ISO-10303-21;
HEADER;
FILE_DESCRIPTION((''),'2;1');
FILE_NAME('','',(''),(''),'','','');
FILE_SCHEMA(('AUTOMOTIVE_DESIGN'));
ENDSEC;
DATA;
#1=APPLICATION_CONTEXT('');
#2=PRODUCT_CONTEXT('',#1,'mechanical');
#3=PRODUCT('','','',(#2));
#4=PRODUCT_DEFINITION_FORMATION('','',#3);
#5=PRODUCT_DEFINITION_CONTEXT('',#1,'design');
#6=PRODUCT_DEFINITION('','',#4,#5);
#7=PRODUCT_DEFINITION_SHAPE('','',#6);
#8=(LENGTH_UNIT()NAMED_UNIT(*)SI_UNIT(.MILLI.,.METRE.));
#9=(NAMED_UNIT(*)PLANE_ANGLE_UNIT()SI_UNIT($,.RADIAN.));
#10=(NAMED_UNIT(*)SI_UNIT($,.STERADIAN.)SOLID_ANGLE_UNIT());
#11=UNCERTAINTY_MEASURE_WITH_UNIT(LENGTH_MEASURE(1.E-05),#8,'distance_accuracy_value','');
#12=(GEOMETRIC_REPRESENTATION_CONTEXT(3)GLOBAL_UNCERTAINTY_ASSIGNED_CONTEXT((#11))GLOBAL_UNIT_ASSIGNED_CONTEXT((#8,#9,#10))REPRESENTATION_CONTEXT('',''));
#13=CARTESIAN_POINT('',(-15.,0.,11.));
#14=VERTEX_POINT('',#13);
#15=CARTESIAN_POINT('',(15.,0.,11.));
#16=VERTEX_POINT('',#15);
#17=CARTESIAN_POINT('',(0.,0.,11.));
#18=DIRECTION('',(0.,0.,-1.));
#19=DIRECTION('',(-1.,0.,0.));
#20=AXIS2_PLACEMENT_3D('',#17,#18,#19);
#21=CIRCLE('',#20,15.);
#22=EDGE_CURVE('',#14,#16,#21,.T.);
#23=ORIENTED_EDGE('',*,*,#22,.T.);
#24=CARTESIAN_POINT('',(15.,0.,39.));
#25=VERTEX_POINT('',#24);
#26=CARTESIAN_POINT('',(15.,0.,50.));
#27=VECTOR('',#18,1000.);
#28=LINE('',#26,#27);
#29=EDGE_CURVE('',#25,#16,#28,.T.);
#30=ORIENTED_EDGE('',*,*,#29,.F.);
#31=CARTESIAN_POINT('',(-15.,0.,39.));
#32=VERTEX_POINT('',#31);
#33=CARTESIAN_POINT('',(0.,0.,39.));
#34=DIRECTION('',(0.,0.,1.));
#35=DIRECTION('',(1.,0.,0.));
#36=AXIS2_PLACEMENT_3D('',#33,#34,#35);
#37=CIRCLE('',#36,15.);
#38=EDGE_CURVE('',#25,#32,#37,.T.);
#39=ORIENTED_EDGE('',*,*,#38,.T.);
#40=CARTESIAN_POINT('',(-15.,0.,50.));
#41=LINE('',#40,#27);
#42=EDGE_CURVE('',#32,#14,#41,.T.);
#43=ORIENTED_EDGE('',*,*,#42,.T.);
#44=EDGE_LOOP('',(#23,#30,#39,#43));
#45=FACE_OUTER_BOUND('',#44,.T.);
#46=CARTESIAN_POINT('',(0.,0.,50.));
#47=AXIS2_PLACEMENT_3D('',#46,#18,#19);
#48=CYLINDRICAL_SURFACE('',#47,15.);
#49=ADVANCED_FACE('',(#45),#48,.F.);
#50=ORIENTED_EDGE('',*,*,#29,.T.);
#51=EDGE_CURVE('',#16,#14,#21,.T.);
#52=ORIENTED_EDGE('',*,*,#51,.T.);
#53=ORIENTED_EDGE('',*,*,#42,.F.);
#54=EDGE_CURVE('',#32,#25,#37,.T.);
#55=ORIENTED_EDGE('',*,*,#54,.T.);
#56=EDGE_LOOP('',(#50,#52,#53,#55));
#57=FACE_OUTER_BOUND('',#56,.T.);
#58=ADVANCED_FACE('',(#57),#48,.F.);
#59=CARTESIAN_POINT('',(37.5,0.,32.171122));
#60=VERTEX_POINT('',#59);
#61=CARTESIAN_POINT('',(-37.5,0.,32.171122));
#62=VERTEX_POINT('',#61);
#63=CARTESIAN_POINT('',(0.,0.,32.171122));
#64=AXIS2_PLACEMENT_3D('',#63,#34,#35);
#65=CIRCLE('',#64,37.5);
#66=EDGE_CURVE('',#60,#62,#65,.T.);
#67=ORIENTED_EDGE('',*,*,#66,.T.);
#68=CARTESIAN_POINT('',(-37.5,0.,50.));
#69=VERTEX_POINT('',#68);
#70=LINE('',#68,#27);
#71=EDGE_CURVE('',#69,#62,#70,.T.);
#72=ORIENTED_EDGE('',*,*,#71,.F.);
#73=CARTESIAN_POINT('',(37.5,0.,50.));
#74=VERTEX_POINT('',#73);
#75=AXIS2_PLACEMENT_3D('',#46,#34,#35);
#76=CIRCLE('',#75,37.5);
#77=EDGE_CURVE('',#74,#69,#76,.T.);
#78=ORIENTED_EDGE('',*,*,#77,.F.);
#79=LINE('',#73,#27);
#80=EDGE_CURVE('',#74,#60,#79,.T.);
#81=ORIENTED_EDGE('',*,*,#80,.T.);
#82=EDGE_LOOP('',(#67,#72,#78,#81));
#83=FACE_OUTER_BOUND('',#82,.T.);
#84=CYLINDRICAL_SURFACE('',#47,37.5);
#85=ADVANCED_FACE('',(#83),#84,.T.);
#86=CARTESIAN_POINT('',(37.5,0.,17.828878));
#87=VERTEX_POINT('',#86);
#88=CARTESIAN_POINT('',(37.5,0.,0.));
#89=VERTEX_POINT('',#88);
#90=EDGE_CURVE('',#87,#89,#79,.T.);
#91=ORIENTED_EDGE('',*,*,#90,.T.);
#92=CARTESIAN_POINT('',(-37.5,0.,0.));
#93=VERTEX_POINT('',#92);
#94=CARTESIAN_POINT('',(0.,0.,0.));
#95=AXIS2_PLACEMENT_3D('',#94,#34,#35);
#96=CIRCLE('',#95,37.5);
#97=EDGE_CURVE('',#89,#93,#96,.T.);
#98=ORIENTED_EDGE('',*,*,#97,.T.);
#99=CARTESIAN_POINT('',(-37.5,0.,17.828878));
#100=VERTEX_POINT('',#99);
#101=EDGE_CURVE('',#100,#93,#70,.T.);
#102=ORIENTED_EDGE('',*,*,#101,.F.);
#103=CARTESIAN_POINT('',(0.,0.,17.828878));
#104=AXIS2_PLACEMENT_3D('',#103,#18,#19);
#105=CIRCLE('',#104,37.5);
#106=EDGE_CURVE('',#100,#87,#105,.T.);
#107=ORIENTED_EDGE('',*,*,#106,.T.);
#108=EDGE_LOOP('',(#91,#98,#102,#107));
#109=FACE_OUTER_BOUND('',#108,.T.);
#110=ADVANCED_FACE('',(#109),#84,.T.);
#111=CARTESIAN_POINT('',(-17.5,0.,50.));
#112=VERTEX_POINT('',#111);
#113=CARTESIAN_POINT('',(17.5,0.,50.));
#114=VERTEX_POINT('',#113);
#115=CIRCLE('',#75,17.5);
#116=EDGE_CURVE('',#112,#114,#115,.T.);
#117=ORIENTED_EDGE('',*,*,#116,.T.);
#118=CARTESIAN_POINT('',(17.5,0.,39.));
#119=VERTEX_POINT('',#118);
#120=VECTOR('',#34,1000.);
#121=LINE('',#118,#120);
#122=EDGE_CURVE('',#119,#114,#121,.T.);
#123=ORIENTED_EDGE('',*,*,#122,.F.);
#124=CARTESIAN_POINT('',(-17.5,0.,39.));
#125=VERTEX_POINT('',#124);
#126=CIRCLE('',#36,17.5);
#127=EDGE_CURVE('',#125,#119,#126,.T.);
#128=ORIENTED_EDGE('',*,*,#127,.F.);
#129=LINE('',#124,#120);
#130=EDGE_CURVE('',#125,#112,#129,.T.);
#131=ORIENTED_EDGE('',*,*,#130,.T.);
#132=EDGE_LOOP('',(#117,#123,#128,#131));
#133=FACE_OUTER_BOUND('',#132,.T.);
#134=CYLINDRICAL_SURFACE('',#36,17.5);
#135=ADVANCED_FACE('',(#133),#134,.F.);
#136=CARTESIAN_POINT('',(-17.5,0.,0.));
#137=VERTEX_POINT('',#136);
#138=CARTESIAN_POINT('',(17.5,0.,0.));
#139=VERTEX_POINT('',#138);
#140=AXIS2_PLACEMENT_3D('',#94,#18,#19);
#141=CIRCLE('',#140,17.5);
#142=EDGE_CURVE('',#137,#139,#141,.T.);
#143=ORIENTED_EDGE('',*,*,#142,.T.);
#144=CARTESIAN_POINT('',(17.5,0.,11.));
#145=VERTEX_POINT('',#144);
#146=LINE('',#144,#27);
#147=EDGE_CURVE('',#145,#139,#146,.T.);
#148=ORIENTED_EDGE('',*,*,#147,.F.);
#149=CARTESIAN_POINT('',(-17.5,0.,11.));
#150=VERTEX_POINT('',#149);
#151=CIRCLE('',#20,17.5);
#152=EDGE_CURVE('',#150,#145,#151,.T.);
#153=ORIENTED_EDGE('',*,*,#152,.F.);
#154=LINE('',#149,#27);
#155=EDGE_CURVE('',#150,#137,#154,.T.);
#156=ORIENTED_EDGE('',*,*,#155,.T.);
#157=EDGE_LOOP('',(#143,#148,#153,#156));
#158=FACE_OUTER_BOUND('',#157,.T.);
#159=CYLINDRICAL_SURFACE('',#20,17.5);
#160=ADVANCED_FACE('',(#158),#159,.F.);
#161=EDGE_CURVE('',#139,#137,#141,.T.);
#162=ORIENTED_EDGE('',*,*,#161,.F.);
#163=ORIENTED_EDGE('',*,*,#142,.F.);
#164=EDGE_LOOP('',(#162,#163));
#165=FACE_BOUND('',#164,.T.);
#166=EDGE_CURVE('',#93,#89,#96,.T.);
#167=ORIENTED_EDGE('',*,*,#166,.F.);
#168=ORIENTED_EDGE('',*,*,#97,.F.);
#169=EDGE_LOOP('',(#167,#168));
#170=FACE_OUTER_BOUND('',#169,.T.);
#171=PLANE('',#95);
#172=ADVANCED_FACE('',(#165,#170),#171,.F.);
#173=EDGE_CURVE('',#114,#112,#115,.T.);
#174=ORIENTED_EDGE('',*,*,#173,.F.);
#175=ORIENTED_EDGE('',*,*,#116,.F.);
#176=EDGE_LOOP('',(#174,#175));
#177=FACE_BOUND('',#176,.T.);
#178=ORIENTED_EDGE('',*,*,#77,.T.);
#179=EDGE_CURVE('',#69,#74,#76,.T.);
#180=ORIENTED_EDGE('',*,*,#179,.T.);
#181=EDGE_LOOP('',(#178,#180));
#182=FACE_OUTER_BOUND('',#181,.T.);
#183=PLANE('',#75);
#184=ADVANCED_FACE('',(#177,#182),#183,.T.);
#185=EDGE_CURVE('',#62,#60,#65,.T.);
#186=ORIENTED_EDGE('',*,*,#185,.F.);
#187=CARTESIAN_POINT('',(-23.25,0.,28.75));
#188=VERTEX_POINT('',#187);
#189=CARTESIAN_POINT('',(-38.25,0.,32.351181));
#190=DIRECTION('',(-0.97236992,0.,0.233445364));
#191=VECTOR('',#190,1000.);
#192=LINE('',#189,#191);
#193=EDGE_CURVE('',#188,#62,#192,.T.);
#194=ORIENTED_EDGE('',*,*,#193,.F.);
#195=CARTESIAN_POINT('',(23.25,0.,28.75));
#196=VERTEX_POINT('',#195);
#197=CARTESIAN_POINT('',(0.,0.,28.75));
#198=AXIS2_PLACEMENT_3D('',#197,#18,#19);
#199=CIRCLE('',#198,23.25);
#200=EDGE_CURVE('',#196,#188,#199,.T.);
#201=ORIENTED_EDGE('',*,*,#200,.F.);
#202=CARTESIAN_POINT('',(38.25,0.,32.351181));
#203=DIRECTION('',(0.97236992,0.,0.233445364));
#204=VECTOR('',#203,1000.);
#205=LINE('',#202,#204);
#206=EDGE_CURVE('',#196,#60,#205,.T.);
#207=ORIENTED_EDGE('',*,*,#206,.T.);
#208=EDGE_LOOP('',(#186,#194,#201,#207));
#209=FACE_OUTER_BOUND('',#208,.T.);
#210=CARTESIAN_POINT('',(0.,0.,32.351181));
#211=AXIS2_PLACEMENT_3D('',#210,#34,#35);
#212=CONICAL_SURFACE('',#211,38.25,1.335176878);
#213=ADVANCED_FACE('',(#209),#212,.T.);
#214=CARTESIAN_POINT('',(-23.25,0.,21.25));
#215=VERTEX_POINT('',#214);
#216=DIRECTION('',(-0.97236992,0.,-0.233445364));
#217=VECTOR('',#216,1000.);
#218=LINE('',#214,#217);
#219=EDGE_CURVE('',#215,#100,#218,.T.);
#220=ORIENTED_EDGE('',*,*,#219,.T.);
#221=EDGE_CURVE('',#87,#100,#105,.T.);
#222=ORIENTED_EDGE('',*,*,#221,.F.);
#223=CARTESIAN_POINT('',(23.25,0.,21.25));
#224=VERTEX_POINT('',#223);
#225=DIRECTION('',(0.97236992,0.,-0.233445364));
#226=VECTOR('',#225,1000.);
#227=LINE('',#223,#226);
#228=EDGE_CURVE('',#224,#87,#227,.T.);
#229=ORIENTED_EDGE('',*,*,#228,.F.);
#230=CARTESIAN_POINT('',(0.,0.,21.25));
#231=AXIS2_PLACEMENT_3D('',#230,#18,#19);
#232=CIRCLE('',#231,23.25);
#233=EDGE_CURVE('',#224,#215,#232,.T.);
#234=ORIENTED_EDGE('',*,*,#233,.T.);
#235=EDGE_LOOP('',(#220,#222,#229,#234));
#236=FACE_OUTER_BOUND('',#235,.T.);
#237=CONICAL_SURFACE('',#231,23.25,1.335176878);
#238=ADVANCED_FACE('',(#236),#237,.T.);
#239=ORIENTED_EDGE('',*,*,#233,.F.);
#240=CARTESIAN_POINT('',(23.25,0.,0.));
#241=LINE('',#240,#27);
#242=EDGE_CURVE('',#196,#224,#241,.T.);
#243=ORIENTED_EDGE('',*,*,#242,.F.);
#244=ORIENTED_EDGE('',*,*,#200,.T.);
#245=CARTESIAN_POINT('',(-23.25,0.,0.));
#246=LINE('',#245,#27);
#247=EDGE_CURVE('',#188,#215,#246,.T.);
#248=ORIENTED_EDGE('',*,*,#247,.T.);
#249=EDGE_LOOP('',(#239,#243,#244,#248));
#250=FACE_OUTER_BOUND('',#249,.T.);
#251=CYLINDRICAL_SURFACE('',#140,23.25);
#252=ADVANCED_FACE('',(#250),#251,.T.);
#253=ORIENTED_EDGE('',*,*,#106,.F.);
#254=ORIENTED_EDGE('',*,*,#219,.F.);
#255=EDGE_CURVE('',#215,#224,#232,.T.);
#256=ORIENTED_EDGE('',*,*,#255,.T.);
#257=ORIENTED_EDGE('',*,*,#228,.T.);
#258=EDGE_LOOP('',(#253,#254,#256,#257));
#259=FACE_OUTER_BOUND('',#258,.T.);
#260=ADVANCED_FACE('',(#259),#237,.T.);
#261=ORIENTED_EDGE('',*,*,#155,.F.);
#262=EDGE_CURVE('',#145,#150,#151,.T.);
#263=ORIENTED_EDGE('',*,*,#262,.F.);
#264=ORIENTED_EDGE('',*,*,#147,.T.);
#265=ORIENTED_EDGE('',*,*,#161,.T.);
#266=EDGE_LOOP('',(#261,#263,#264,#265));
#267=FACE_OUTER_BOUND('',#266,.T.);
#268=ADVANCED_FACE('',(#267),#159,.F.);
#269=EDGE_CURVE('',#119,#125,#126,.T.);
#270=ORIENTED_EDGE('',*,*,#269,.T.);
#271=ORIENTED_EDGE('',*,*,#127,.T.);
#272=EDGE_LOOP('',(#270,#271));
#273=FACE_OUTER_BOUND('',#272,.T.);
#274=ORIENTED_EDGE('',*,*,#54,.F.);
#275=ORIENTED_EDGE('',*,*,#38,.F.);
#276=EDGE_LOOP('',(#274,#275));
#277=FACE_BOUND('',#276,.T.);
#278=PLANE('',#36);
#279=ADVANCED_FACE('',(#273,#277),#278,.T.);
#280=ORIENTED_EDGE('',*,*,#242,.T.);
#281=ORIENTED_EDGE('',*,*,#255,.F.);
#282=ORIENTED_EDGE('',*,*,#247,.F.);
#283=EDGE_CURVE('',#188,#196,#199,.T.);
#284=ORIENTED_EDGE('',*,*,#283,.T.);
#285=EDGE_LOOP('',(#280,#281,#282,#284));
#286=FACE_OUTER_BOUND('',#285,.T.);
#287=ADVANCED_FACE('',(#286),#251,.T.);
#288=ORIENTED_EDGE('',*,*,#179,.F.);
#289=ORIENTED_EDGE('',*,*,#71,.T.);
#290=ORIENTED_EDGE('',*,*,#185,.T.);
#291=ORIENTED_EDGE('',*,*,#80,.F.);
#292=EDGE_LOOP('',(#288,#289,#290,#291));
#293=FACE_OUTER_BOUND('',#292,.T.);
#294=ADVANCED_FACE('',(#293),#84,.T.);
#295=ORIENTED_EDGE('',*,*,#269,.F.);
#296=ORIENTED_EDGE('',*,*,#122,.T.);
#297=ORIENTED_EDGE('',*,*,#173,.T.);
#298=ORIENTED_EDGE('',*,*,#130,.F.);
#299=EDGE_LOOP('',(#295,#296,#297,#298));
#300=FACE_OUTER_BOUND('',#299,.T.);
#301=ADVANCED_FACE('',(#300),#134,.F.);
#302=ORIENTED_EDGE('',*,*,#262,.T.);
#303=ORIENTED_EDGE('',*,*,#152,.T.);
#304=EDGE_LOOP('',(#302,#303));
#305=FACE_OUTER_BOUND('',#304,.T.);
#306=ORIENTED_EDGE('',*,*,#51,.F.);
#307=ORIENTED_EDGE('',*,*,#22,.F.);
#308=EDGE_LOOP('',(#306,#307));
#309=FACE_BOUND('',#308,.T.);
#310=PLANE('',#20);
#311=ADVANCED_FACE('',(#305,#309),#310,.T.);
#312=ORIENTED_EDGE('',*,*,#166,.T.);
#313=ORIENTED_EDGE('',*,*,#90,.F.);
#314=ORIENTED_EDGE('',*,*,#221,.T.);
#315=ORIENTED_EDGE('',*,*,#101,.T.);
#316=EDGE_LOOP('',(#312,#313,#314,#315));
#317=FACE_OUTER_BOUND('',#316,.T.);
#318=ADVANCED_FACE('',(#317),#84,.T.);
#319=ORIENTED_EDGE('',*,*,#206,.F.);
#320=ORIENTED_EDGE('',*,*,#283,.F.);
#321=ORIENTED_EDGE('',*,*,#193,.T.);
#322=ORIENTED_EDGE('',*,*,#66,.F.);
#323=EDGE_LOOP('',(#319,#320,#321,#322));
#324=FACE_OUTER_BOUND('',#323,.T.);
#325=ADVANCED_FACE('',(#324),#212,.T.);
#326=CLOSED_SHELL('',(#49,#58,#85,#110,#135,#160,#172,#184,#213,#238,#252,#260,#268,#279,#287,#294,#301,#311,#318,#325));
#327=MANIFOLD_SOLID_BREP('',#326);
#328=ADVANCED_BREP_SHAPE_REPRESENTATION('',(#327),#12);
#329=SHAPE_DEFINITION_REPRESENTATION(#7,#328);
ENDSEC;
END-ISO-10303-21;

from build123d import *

# Parameters (mm, degrees)
SKETCH_1_R          = 37.5
SKETCH_1_R_2        = 15
EXTRUDE_1_DEPTH     = 50
SKETCH_3_R          = 17.5
CUT_EXTRUDE_1_DEPTH = 11
CUT_EXTRUDE_START   = -11
SKETCH_4_R          = 17.5
CUT_EXTRUDE_2_DEPTH = 11


with BuildPart() as part:
    # 草图1 → 凸台-拉伸1 (new body)
    with BuildSketch(Plane.XY):
        Circle(SKETCH_1_R)
        Circle(SKETCH_1_R_2, mode=Mode.SUBTRACT)
    extrude(amount=EXTRUDE_1_DEPTH)

    # 草图2 → 切除-旋转1 (revolve, cut)
    with BuildSketch(Plane(origin=(0, 0, 0), x_dir=(1, 0, 0), z_dir=(0, 1, 0))):
        Polygon((-38.25, -17.648818614), (-23.25, -21.25), (-23.25, -28.75), (-38.25, -32.351181386), align=None)
    revolve(axis=Axis((0, 0, 0), (0, 0, 1)), mode=Mode.SUBTRACT)

    # 草图3 → 切除-拉伸1 (cut)
    with BuildSketch(Plane.XY.offset(50)):
        Circle(SKETCH_3_R)
    extrude(amount=-CUT_EXTRUDE_1_DEPTH, mode=Mode.SUBTRACT)

    # 草图4 → 切除-拉伸2 (cut)
    with BuildSketch(Plane(origin=(0, 0, 0), x_dir=(-1, 0, 0), z_dir=(0, 0, -1)).offset(CUT_EXTRUDE_START)):
        with Locations(Location((0, 0, 0), (0, 0, 180))):
            Circle(SKETCH_4_R)
    extrude(amount=CUT_EXTRUDE_2_DEPTH, mode=Mode.SUBTRACT)


solid = part.part
